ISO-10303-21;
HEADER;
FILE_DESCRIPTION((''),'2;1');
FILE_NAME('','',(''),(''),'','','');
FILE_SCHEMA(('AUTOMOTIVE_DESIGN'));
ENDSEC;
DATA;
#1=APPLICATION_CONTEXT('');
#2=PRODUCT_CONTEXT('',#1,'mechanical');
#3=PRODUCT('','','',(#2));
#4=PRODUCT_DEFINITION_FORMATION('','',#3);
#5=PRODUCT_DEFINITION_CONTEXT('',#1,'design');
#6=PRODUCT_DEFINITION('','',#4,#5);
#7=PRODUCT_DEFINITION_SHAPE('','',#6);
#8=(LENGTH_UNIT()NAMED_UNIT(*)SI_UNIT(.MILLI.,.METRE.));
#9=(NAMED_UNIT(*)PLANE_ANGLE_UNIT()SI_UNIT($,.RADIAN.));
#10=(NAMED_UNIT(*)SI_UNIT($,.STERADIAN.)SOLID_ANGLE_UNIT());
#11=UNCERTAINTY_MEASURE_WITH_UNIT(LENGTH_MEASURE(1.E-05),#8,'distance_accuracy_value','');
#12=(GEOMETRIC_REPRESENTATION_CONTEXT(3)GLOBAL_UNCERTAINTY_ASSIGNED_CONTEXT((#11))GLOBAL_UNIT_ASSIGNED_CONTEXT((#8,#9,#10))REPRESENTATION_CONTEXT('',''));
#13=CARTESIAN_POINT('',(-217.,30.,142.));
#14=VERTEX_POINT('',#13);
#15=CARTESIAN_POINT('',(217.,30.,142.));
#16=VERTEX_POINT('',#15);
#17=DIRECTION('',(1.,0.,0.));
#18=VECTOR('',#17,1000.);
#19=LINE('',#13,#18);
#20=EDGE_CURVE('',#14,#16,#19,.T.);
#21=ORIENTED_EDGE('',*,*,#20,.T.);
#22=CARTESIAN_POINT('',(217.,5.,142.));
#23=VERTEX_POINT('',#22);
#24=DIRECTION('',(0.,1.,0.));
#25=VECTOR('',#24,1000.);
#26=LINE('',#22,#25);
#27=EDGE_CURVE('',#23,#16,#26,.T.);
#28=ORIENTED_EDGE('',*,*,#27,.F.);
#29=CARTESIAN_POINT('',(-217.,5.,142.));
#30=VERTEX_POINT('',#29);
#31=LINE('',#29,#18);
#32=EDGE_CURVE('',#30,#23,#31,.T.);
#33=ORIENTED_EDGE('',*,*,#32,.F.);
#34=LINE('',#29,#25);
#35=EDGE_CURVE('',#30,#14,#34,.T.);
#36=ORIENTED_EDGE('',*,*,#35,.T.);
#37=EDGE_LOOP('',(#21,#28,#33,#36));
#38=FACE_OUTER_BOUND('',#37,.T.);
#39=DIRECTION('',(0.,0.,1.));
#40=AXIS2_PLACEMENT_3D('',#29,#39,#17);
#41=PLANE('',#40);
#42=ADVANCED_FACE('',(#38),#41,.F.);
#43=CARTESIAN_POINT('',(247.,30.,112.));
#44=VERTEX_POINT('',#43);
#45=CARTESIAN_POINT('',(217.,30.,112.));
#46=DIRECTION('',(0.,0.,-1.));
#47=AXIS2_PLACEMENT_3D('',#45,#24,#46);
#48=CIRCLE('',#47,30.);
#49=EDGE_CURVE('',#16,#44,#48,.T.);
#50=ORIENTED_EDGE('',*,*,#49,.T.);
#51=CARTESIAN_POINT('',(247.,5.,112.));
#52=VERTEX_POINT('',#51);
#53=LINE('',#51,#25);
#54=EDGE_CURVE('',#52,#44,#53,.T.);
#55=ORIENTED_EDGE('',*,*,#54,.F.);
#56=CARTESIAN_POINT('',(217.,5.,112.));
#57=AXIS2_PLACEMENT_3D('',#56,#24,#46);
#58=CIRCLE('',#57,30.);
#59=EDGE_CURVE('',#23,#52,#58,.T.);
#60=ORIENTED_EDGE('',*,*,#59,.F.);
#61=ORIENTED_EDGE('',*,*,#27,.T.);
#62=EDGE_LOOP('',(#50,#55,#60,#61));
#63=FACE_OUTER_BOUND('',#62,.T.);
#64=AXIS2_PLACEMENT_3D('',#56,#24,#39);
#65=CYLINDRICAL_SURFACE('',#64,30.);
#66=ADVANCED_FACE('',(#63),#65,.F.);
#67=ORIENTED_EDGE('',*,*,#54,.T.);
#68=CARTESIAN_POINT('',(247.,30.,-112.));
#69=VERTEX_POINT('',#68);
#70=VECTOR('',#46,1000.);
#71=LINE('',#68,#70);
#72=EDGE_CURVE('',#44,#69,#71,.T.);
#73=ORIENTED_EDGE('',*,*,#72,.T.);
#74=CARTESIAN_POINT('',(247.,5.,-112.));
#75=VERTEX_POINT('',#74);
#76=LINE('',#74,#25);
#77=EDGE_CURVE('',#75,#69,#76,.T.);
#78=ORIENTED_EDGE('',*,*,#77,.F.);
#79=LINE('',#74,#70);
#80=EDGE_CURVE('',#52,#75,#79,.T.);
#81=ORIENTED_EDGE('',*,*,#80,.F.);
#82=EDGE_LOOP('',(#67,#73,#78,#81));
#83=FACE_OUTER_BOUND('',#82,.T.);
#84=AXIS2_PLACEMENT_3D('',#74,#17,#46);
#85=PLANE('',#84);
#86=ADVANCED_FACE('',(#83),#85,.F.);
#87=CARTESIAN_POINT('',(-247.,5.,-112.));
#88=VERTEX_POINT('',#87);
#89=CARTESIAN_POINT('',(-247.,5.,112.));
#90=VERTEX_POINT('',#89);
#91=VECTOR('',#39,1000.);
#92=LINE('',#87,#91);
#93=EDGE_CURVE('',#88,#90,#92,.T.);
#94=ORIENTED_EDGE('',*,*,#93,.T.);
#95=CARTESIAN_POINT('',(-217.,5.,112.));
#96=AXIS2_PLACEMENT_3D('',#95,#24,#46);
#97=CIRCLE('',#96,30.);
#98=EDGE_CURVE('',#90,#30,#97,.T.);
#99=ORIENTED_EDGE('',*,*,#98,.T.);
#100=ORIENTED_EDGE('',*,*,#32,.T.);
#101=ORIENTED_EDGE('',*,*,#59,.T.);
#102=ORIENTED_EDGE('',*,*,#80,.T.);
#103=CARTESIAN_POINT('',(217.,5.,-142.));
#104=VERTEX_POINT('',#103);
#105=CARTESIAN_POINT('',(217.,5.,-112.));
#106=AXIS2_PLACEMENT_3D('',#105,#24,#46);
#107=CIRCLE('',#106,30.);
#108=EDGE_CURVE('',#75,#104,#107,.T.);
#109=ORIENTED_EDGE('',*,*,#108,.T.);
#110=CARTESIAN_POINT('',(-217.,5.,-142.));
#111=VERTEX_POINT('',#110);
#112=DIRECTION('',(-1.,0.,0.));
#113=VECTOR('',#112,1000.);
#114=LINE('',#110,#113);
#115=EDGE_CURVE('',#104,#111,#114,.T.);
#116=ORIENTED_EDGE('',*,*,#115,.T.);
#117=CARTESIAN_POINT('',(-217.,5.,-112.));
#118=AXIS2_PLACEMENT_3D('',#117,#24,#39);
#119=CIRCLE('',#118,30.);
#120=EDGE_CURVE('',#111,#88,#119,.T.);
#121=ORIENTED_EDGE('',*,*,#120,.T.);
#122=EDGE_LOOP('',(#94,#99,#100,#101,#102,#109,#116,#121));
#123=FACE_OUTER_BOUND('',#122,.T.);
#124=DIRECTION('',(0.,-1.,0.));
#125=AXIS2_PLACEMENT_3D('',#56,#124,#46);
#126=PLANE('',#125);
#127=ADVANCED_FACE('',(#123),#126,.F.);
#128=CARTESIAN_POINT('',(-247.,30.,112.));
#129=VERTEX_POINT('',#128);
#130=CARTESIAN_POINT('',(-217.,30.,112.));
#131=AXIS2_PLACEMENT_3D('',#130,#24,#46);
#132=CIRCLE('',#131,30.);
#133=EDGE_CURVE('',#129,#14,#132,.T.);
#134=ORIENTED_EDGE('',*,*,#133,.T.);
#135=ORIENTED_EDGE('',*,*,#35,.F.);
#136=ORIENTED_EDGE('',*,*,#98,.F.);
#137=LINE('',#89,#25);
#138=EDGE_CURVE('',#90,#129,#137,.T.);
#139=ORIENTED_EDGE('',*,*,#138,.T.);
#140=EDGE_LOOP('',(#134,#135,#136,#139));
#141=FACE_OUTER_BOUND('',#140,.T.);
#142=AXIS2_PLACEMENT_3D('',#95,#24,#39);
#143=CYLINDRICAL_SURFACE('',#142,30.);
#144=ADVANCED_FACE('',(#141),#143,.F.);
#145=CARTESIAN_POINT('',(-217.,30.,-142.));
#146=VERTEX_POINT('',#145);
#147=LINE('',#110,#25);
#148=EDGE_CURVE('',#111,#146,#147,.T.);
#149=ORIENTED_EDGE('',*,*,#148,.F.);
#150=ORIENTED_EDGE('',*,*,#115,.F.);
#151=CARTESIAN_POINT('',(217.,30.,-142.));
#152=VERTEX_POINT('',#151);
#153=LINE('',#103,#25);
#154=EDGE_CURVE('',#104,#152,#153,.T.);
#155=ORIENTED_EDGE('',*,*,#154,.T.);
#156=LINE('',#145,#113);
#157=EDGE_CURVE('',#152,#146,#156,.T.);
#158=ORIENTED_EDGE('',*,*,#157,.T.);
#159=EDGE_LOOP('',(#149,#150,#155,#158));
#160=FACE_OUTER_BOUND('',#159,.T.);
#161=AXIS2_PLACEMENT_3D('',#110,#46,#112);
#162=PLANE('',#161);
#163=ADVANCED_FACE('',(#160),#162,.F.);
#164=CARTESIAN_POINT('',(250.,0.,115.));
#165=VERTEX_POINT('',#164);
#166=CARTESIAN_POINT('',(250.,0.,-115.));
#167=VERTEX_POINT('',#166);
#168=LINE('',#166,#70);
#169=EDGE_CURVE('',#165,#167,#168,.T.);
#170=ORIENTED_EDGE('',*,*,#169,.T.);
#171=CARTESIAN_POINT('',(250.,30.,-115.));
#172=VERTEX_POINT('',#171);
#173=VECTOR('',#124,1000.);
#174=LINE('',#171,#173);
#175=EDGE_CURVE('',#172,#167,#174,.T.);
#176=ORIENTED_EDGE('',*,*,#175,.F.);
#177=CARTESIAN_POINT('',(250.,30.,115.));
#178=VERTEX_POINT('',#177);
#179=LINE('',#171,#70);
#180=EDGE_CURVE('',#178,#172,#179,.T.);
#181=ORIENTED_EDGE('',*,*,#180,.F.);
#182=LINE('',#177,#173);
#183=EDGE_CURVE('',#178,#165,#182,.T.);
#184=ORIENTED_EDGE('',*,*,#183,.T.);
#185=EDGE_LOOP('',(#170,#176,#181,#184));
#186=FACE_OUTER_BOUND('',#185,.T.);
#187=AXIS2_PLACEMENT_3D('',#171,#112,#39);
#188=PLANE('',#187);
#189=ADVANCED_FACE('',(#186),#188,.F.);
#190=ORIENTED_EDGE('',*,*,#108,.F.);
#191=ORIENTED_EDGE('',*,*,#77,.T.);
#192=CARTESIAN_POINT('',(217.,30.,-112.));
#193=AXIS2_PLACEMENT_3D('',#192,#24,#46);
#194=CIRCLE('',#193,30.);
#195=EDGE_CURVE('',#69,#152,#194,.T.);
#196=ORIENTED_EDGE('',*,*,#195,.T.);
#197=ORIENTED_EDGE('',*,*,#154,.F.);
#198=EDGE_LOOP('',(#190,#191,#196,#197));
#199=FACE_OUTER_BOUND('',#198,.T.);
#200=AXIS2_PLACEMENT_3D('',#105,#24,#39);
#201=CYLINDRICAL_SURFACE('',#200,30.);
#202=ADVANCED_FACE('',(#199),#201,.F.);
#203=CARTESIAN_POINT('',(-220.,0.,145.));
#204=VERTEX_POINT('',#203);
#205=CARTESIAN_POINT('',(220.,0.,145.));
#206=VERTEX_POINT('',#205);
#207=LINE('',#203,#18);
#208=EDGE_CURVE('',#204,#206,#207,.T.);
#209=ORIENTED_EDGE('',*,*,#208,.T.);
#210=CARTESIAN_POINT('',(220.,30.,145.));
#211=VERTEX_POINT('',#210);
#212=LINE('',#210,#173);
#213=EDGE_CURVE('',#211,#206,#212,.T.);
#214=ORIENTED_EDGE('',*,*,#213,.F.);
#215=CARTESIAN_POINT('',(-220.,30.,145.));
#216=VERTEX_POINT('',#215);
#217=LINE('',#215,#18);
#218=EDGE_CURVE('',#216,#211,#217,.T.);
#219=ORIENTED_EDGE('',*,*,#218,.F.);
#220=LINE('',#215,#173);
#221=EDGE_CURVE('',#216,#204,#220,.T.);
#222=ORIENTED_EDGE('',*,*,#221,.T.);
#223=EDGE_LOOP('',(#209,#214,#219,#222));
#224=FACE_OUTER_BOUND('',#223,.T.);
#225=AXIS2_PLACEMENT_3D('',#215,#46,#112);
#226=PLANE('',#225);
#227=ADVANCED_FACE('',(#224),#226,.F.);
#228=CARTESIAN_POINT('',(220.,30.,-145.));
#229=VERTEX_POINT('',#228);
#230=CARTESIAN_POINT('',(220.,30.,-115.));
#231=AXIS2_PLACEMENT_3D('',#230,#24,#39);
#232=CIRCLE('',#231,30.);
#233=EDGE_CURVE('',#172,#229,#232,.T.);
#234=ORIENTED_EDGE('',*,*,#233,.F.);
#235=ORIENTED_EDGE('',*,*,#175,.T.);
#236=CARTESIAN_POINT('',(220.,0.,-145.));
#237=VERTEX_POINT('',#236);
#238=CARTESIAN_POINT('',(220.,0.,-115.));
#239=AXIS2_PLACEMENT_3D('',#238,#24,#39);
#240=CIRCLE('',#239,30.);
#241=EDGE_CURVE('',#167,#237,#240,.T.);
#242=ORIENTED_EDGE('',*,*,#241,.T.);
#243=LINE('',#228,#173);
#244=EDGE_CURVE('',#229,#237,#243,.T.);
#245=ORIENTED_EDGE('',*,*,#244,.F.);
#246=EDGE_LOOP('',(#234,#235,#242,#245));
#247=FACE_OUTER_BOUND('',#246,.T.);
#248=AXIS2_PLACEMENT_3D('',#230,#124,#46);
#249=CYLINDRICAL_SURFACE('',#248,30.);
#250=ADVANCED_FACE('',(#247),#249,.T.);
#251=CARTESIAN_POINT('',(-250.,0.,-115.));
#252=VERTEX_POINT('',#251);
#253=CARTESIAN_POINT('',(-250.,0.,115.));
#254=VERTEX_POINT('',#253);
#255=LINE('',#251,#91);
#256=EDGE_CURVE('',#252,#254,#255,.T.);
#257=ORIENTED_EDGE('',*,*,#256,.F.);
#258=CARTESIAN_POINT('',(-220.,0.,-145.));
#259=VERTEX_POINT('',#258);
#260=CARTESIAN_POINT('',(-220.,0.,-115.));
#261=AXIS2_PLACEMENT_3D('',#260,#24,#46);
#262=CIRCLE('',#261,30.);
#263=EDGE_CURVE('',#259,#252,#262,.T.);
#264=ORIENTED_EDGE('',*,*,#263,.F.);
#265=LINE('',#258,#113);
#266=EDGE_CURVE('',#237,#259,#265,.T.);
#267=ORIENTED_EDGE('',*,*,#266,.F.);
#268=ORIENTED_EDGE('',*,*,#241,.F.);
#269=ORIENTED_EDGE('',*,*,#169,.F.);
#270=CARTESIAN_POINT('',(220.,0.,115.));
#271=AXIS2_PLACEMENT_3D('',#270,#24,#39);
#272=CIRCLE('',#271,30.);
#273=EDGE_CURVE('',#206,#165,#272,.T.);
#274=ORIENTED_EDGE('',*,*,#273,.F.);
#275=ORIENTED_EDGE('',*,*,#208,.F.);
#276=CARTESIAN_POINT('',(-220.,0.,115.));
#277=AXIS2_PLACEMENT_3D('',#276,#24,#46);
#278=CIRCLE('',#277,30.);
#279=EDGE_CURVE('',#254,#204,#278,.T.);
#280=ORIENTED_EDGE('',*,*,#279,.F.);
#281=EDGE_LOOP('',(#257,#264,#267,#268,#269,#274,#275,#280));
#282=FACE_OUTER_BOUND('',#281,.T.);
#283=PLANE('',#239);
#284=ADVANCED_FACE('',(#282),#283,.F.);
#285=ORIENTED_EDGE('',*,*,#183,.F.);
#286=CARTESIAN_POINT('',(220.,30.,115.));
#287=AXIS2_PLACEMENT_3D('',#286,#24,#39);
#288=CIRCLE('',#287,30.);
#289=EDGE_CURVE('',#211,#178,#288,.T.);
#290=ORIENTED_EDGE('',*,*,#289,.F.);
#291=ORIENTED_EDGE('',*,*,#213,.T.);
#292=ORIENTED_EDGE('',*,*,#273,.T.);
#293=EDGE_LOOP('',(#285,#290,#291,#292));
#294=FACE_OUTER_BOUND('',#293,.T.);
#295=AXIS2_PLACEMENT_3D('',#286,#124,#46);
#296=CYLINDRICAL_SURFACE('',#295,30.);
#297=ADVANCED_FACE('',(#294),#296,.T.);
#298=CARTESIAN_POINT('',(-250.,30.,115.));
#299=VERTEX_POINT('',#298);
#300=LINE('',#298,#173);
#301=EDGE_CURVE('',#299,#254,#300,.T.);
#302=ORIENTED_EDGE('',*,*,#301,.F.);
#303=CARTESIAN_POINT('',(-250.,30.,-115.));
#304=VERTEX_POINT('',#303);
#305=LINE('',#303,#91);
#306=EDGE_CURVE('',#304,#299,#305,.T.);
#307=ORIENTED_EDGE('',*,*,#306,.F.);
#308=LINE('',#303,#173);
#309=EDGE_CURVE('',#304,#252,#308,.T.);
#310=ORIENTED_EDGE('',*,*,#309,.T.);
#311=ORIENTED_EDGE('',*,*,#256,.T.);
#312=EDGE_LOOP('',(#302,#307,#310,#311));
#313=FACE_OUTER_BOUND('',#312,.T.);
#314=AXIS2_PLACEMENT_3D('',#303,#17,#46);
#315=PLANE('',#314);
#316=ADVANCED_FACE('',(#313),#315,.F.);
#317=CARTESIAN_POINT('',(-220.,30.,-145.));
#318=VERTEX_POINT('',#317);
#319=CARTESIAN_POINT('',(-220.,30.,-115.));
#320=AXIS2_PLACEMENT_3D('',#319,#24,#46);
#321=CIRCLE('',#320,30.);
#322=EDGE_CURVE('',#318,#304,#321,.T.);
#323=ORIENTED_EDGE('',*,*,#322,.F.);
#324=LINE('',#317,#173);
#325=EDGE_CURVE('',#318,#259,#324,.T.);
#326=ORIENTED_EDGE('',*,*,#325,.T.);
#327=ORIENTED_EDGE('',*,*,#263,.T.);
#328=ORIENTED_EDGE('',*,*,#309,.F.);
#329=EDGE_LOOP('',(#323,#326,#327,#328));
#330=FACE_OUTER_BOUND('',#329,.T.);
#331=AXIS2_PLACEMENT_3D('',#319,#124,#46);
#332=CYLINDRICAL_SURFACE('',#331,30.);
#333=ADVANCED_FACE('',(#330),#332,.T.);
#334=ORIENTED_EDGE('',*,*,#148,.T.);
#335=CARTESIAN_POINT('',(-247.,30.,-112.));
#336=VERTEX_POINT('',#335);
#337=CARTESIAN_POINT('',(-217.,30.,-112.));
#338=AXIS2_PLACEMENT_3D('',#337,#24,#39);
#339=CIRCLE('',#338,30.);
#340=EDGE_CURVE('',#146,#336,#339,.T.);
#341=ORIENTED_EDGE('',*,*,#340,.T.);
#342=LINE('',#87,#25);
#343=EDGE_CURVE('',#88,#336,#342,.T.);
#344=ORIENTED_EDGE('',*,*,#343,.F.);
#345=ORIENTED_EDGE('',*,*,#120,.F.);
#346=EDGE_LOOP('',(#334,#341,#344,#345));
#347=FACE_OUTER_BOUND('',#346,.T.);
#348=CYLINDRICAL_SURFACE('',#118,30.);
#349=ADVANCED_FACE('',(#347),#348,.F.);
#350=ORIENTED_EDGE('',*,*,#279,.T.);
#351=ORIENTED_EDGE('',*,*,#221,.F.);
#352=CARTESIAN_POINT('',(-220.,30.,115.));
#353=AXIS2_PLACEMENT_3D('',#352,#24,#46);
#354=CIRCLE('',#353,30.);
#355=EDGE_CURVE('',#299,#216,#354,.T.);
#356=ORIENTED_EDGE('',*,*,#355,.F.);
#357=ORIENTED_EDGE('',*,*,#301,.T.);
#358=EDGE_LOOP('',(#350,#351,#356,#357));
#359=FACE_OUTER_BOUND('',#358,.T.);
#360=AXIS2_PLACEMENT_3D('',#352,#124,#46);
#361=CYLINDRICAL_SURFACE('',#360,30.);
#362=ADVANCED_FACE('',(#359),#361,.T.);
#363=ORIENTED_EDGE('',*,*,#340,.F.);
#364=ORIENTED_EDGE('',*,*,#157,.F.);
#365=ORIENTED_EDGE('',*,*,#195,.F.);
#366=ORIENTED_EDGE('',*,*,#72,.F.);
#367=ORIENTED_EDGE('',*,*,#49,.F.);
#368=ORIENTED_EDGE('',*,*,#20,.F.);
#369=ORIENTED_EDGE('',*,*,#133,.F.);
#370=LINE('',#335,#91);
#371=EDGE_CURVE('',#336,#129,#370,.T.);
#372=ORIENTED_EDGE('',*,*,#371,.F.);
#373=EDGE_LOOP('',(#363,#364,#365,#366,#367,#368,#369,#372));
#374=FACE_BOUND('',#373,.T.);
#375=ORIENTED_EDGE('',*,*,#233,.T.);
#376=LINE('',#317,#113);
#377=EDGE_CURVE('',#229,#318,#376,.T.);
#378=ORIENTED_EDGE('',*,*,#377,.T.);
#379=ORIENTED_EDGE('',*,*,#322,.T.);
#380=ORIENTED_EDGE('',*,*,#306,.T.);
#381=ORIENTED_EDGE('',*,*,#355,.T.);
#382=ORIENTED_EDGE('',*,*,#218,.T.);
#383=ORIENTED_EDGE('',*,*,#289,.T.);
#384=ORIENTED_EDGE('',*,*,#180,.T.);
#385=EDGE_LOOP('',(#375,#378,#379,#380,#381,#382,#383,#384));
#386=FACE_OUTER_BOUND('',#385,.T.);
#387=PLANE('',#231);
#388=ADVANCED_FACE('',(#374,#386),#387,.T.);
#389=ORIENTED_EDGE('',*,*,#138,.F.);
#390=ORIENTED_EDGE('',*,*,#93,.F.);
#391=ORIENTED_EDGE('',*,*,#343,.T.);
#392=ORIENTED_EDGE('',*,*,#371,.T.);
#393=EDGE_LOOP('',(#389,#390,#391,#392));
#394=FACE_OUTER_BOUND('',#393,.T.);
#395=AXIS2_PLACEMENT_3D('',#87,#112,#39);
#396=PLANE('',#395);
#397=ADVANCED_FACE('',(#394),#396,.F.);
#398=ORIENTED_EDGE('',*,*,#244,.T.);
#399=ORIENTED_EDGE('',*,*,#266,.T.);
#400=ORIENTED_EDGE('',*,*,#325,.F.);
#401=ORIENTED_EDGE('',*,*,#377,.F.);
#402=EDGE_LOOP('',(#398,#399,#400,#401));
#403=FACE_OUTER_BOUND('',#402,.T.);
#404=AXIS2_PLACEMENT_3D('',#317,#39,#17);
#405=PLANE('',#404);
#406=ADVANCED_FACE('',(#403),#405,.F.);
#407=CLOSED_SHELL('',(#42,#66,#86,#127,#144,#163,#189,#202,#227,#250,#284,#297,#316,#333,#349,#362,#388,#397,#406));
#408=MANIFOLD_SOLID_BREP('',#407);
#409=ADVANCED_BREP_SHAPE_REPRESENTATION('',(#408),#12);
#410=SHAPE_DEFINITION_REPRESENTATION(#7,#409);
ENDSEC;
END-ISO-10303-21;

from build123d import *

# Parameters (mm, degrees)
BOSS_EXTRUDE1_DEPTH = 30
CUT_EXTRUDE1_DEPTH  = 25


with BuildPart() as part:
    # Sketch1 → Boss-Extrude1 (new body)
    with BuildSketch(Plane(origin=(0, 0, 0), x_dir=(1, 0, 0), z_dir=(0, 1, 0))):
        with BuildLine():
            Line((-220, 145), (220, 145))
            ThreePointArc((220, 145), (241.213203436, 136.213203436), (250, 115))
            Line((250, 115), (250, -115))
            ThreePointArc((250, -115), (241.213203436, -136.213203436), (220, -145))
            Line((220, -145), (-220, -145))
            ThreePointArc((-220, -145), (-241.213203436, -136.213203436), (-250, -115))
            Line((-250, -115), (-250, 115))
            ThreePointArc((-250, 115), (-241.213203436, 136.213203436), (-220, 145))
        make_face()
    extrude(amount=BOSS_EXTRUDE1_DEPTH)

    # Sketch2 → Cut-Extrude1 (cut)
    with BuildSketch(Plane(origin=(0, 30, 0), x_dir=(1, 0, 0), z_dir=(0, 1, 0))):
        with BuildLine():
            Line((-217, 142), (217, 142))
            ThreePointArc((217, 142), (238.213203436, 133.213203436), (247, 112))
            Line((247, 112), (247, -112))
            ThreePointArc((247, -112), (238.213203436, -133.213203436), (217, -142))
            Line((217, -142), (-217, -142))
            ThreePointArc((-217, -142), (-238.213203436, -133.213203436), (-247, -112))
            Line((-247, -112), (-247, 112))
            ThreePointArc((-247, 112), (-238.213203436, 133.213203436), (-217, 142))
        make_face()
    extrude(amount=-CUT_EXTRUDE1_DEPTH, mode=Mode.SUBTRACT)


solid = part.part
